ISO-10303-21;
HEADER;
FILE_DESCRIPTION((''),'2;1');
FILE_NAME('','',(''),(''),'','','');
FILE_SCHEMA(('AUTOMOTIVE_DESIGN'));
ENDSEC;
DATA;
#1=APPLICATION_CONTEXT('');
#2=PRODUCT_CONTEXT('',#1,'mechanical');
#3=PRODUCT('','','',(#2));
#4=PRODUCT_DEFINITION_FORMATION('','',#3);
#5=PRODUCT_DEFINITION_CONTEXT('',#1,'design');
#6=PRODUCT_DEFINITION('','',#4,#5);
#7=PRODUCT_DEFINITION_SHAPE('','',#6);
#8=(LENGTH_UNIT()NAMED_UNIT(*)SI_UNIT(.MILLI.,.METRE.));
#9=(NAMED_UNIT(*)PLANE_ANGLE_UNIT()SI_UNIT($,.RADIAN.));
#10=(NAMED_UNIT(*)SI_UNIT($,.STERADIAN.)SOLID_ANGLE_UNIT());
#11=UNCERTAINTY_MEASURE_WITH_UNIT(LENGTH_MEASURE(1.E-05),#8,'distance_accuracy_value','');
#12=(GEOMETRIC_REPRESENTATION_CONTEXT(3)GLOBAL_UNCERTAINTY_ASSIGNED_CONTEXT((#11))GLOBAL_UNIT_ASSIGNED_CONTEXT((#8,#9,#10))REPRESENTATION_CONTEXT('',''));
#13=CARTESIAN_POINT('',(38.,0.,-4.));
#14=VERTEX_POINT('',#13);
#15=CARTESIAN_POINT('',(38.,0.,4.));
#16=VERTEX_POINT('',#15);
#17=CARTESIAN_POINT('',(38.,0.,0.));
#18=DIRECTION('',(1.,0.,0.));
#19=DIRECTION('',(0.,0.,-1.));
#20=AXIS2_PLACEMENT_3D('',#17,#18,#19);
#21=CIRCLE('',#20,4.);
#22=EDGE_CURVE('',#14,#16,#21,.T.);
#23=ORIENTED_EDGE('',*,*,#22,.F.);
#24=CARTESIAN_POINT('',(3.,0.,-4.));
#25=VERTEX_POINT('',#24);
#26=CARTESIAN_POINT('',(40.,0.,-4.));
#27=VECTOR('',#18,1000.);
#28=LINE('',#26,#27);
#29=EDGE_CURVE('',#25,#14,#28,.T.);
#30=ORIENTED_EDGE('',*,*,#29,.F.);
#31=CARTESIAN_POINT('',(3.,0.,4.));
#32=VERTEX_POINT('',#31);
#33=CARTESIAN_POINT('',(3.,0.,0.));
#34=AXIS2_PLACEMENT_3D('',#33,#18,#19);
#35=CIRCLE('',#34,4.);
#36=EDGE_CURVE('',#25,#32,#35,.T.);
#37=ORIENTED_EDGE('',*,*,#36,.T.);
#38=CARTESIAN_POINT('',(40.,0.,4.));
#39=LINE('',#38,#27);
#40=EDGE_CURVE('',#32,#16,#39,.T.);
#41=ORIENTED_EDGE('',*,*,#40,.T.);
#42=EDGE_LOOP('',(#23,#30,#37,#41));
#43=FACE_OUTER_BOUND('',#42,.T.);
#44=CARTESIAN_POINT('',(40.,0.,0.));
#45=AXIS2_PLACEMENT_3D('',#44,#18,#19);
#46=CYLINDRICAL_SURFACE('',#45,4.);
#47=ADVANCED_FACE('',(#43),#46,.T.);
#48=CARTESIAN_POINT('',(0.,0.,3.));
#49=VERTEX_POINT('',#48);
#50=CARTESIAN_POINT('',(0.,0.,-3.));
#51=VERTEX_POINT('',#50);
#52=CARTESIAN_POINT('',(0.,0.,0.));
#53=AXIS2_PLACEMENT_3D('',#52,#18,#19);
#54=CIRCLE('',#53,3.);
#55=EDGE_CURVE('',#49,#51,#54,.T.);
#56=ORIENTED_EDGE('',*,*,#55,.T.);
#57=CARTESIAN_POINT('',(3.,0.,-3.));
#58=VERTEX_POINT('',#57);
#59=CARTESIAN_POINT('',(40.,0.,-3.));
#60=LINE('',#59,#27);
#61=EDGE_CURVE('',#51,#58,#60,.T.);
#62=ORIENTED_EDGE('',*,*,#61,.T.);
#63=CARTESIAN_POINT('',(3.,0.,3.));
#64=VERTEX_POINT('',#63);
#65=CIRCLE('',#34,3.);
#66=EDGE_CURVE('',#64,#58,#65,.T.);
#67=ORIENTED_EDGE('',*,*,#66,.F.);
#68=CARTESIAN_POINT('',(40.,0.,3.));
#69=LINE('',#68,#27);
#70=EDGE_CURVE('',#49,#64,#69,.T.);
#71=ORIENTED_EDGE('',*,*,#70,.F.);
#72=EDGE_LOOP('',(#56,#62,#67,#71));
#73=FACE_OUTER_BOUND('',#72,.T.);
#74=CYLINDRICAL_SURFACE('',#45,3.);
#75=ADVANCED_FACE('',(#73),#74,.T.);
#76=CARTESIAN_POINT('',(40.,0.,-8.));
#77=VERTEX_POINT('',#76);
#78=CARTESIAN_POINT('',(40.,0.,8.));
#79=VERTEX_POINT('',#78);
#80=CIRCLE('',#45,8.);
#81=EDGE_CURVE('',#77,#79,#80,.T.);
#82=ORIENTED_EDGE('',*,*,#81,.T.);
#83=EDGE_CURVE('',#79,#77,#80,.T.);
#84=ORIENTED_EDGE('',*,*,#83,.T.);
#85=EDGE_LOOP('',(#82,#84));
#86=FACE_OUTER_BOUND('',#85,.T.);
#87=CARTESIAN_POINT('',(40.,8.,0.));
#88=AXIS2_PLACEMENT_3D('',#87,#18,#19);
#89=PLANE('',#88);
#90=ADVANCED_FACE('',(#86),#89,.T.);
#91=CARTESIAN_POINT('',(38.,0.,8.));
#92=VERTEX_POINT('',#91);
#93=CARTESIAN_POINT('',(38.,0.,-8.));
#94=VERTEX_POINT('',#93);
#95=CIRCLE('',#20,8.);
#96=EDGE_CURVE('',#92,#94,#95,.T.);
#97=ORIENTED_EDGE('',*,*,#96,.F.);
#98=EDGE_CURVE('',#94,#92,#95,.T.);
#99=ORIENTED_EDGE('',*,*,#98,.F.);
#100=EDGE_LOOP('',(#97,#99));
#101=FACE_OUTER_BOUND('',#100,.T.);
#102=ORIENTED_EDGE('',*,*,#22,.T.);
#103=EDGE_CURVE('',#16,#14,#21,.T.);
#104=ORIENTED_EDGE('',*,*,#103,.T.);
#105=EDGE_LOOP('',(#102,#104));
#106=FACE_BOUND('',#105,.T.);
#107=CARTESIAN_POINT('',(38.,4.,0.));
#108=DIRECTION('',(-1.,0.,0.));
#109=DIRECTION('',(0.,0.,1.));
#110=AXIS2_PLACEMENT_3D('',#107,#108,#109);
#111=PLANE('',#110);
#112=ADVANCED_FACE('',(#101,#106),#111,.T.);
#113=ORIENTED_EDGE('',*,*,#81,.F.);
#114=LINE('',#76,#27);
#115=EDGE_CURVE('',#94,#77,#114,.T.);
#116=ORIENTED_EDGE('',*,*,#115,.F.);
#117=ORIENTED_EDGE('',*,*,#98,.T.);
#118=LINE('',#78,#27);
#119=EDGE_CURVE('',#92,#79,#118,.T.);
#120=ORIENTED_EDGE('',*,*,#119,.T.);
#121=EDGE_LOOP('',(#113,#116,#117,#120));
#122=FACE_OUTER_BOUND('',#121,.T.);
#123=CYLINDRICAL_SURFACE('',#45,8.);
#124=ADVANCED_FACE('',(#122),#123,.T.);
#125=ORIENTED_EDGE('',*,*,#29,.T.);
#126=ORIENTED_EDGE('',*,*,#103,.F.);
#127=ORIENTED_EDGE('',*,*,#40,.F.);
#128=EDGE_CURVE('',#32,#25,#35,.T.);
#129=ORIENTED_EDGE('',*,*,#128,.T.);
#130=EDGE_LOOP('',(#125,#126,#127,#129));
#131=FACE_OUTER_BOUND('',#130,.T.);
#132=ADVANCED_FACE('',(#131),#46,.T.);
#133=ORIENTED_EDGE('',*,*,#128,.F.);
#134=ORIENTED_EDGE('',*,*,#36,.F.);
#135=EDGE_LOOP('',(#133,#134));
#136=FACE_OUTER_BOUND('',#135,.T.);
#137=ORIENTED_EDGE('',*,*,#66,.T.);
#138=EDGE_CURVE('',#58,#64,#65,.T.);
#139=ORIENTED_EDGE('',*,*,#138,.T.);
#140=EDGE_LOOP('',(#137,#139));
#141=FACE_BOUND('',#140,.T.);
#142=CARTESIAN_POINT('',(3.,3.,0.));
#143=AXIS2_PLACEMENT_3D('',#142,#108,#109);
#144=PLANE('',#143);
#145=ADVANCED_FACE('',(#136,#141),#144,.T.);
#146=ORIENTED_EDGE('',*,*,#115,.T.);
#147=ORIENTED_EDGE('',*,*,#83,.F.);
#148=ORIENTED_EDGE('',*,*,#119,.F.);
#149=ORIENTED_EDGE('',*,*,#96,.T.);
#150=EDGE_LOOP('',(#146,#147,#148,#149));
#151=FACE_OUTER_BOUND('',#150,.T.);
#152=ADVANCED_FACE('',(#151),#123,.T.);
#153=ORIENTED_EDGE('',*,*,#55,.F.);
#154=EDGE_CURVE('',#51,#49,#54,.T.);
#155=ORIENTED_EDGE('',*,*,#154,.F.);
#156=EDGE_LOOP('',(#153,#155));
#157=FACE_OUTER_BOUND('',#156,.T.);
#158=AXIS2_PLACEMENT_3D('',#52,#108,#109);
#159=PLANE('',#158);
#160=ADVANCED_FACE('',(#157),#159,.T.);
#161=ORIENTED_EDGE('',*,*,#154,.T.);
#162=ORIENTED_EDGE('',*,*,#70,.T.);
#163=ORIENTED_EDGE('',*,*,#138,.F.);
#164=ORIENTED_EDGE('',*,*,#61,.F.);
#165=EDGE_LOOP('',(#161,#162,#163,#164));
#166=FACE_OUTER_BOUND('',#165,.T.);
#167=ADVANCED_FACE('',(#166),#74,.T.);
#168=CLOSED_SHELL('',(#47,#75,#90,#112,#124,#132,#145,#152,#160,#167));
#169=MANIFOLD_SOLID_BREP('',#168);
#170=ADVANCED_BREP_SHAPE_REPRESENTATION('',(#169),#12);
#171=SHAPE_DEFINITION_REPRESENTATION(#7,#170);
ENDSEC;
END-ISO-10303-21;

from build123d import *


with BuildPart() as part:
    # Sketch1 → Revolve1 (revolve)
    with BuildSketch(Plane.XY, mode=Mode.PRIVATE) as revolve1_sk:
        Polygon((0, 0), (0, 3), (3, 3), (3, 4), (38, 4), (38, 8), (40, 8), (40, 0), align=None)
    revolve(revolve1_sk.sketch.rotate(Axis((40, 0, 0), (-1, 0, 0)), 90), axis=Axis((40, 0, 0), (-1, 0, 0)))


solid = part.part
